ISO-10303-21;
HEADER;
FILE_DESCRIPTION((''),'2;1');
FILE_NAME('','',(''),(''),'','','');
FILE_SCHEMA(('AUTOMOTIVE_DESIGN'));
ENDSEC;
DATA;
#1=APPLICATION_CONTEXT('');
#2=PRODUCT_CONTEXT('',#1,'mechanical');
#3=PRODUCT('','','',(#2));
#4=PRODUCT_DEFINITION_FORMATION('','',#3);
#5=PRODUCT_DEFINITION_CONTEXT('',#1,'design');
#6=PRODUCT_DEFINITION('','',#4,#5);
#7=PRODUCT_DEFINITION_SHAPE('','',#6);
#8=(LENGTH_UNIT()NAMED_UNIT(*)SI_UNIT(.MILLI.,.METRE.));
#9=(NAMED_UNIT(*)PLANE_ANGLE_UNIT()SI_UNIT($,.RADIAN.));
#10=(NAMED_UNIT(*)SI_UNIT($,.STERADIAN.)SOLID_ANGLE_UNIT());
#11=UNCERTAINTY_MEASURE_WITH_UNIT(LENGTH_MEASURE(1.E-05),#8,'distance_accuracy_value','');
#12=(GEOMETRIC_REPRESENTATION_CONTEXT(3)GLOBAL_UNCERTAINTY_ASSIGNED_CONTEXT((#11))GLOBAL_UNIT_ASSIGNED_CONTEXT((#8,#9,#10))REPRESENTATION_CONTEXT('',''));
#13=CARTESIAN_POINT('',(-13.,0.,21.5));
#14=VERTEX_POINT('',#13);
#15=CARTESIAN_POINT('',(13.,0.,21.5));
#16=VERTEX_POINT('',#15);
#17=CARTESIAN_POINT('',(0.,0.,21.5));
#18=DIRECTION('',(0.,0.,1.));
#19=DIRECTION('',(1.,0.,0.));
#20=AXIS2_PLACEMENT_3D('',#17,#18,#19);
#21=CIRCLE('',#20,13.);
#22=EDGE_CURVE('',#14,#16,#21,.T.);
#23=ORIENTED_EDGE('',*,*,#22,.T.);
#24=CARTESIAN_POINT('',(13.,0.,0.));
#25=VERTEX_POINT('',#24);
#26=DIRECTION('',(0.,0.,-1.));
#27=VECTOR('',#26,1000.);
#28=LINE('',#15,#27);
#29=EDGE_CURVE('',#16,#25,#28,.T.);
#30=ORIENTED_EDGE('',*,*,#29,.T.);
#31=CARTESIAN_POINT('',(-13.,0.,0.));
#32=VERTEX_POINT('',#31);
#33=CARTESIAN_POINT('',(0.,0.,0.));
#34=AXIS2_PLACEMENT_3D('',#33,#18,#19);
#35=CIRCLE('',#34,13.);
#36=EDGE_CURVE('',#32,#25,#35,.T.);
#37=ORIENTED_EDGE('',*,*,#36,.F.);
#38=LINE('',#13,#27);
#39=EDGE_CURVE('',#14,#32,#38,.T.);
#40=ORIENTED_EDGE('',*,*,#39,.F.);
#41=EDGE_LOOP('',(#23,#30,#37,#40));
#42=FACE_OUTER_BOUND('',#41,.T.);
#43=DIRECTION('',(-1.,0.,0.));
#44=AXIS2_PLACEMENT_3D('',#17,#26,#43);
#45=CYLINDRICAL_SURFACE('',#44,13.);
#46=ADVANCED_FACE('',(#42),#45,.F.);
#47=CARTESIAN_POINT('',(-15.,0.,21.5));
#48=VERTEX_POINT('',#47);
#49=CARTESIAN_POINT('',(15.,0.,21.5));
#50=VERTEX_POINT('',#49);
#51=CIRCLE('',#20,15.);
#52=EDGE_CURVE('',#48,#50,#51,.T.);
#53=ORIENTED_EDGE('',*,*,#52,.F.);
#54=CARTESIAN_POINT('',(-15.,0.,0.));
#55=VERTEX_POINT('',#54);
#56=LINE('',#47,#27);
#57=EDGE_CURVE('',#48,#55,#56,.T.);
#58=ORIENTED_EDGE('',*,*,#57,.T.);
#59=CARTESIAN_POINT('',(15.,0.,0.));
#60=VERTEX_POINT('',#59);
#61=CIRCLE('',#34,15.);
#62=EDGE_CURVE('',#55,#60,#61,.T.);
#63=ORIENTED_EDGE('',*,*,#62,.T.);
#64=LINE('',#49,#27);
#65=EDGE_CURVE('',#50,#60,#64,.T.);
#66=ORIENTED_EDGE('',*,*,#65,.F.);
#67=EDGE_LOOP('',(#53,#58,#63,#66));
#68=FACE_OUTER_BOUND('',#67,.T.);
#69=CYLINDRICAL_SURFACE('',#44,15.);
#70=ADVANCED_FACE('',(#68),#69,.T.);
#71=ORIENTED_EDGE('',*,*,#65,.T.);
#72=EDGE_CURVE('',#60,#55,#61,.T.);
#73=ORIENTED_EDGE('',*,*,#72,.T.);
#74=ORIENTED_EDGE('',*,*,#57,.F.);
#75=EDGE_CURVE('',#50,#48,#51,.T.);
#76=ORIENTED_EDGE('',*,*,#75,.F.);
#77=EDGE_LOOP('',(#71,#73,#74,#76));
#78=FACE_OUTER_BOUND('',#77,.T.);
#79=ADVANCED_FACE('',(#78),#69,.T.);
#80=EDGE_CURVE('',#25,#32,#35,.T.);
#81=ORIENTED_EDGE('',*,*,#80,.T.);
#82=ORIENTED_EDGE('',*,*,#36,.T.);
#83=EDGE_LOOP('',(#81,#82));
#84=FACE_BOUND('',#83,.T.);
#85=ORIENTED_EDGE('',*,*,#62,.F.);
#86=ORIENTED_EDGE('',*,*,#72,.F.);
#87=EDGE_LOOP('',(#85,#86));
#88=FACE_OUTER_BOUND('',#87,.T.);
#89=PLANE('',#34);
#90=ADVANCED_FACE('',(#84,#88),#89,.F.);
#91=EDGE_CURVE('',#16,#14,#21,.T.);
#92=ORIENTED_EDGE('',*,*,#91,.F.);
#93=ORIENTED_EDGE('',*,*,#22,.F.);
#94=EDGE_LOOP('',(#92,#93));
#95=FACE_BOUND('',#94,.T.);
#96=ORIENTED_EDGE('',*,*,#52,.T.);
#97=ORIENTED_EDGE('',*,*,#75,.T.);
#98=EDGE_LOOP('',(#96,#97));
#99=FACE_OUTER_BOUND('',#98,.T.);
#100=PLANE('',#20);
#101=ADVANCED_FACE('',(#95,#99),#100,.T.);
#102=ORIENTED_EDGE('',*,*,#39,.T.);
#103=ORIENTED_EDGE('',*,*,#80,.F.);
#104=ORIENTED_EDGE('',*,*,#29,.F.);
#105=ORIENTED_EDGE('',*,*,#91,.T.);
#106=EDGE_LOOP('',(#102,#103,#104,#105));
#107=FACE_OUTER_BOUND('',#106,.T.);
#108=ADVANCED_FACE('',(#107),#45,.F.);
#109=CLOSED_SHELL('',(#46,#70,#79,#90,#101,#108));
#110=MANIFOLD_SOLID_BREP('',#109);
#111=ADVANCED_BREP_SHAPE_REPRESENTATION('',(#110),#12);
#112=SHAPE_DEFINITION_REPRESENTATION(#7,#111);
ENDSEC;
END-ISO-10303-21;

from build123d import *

# Parameters (mm, degrees)
SKETCH1_R           = 15
SKETCH1_R_2         = 13
BOSS_EXTRUDE1_DEPTH = 21.5


with BuildPart() as part:
    # Sketch1 → Boss-Extrude1 (new body)
    with BuildSketch(Plane.XY):
        Circle(SKETCH1_R)
        Circle(SKETCH1_R_2, mode=Mode.SUBTRACT)
    extrude(amount=BOSS_EXTRUDE1_DEPTH)


solid = part.part
